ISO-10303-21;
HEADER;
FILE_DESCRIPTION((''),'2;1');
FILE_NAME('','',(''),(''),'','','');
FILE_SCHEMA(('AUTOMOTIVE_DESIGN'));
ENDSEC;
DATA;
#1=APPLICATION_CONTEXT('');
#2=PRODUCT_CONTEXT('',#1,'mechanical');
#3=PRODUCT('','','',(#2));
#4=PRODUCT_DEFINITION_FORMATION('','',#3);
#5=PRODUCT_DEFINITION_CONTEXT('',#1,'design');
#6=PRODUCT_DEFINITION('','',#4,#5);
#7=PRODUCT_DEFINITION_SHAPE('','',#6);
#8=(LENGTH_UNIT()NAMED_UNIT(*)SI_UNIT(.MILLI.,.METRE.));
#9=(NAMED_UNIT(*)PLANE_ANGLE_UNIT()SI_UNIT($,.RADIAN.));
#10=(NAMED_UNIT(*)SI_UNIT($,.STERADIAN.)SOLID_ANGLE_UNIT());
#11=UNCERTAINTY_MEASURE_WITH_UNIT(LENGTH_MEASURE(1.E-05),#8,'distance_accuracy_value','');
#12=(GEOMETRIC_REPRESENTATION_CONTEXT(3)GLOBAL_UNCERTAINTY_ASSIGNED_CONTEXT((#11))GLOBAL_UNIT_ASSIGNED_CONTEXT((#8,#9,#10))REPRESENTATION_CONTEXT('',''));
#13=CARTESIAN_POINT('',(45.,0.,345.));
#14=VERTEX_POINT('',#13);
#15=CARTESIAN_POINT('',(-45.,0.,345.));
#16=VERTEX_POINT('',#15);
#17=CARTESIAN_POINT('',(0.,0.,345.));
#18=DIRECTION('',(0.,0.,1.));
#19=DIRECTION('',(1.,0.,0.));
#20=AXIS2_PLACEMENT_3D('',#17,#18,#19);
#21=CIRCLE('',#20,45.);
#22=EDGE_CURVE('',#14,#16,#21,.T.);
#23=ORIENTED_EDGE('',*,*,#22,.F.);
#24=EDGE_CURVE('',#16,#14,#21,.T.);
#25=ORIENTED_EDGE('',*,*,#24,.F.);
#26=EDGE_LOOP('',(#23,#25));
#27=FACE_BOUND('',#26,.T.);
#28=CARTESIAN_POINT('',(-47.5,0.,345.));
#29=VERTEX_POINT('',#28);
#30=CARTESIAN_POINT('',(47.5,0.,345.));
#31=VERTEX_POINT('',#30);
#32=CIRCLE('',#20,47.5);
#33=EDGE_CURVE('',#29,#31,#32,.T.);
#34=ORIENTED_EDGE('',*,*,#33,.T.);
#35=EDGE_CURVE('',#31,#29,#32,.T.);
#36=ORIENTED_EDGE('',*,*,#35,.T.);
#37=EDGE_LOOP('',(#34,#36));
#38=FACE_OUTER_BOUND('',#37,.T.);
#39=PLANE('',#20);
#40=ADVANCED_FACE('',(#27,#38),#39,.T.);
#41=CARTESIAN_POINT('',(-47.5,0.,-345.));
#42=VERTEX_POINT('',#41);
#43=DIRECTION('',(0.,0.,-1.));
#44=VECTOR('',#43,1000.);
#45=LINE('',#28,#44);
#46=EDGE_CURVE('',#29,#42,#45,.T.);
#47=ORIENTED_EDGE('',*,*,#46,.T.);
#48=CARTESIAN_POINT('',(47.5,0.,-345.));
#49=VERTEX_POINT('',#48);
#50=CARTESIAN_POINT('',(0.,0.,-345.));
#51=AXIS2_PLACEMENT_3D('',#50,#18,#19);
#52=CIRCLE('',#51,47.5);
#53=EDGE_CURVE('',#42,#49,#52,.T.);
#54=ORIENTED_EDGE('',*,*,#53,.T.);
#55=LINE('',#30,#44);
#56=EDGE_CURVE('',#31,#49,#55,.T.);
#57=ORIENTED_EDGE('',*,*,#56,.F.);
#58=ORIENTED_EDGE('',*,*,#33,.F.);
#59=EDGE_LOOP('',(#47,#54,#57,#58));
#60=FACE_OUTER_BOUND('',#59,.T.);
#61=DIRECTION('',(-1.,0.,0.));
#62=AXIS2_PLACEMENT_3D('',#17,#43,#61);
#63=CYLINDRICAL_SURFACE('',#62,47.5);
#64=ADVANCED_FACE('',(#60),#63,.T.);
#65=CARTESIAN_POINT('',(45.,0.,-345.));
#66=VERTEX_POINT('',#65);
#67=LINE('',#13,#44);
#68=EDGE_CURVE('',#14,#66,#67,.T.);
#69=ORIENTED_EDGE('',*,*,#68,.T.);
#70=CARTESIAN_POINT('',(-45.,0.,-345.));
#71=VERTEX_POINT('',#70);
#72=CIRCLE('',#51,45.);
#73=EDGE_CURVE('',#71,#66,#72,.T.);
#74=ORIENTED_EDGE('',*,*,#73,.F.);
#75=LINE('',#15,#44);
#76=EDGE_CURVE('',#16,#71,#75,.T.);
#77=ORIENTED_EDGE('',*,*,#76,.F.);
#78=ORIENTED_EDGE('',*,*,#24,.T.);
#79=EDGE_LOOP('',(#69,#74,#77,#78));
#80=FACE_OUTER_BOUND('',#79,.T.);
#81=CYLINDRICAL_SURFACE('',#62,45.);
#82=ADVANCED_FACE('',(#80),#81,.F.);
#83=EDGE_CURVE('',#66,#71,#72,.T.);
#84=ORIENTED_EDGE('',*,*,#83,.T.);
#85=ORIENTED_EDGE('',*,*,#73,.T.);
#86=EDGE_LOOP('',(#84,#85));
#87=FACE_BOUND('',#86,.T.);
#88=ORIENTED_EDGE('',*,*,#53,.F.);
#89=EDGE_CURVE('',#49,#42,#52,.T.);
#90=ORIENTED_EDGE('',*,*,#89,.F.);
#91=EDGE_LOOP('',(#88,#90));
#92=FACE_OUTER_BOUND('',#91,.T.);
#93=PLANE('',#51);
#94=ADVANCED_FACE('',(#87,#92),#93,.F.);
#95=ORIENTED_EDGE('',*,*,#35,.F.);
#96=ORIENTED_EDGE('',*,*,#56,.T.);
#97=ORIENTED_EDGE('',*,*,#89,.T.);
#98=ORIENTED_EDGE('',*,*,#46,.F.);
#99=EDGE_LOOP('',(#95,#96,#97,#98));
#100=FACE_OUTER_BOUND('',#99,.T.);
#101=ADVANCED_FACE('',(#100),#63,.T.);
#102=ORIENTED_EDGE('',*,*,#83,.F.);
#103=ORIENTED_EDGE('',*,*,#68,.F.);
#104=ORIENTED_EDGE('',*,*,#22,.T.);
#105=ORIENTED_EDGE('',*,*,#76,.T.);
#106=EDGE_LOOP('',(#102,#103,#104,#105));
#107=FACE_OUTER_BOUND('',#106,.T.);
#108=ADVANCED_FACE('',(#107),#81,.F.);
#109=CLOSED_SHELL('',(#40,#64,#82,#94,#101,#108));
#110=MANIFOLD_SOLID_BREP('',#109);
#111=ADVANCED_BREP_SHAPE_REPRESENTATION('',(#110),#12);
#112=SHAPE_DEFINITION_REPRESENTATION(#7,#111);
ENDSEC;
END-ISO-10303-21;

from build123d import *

# Parameters (mm, degrees)
SKETCH_1_R      = 47.5
SKETCH_1_R_2    = 45
EXTRUDE_1_DEPTH = 345


with BuildPart() as part:
    # 草图1 → 凸台-拉伸1 (new, symmetric)
    with BuildSketch(Plane.XY):
        Circle(SKETCH_1_R)
        Circle(SKETCH_1_R_2, mode=Mode.SUBTRACT)
    extrude(amount=EXTRUDE_1_DEPTH, both=True)


solid = part.part
